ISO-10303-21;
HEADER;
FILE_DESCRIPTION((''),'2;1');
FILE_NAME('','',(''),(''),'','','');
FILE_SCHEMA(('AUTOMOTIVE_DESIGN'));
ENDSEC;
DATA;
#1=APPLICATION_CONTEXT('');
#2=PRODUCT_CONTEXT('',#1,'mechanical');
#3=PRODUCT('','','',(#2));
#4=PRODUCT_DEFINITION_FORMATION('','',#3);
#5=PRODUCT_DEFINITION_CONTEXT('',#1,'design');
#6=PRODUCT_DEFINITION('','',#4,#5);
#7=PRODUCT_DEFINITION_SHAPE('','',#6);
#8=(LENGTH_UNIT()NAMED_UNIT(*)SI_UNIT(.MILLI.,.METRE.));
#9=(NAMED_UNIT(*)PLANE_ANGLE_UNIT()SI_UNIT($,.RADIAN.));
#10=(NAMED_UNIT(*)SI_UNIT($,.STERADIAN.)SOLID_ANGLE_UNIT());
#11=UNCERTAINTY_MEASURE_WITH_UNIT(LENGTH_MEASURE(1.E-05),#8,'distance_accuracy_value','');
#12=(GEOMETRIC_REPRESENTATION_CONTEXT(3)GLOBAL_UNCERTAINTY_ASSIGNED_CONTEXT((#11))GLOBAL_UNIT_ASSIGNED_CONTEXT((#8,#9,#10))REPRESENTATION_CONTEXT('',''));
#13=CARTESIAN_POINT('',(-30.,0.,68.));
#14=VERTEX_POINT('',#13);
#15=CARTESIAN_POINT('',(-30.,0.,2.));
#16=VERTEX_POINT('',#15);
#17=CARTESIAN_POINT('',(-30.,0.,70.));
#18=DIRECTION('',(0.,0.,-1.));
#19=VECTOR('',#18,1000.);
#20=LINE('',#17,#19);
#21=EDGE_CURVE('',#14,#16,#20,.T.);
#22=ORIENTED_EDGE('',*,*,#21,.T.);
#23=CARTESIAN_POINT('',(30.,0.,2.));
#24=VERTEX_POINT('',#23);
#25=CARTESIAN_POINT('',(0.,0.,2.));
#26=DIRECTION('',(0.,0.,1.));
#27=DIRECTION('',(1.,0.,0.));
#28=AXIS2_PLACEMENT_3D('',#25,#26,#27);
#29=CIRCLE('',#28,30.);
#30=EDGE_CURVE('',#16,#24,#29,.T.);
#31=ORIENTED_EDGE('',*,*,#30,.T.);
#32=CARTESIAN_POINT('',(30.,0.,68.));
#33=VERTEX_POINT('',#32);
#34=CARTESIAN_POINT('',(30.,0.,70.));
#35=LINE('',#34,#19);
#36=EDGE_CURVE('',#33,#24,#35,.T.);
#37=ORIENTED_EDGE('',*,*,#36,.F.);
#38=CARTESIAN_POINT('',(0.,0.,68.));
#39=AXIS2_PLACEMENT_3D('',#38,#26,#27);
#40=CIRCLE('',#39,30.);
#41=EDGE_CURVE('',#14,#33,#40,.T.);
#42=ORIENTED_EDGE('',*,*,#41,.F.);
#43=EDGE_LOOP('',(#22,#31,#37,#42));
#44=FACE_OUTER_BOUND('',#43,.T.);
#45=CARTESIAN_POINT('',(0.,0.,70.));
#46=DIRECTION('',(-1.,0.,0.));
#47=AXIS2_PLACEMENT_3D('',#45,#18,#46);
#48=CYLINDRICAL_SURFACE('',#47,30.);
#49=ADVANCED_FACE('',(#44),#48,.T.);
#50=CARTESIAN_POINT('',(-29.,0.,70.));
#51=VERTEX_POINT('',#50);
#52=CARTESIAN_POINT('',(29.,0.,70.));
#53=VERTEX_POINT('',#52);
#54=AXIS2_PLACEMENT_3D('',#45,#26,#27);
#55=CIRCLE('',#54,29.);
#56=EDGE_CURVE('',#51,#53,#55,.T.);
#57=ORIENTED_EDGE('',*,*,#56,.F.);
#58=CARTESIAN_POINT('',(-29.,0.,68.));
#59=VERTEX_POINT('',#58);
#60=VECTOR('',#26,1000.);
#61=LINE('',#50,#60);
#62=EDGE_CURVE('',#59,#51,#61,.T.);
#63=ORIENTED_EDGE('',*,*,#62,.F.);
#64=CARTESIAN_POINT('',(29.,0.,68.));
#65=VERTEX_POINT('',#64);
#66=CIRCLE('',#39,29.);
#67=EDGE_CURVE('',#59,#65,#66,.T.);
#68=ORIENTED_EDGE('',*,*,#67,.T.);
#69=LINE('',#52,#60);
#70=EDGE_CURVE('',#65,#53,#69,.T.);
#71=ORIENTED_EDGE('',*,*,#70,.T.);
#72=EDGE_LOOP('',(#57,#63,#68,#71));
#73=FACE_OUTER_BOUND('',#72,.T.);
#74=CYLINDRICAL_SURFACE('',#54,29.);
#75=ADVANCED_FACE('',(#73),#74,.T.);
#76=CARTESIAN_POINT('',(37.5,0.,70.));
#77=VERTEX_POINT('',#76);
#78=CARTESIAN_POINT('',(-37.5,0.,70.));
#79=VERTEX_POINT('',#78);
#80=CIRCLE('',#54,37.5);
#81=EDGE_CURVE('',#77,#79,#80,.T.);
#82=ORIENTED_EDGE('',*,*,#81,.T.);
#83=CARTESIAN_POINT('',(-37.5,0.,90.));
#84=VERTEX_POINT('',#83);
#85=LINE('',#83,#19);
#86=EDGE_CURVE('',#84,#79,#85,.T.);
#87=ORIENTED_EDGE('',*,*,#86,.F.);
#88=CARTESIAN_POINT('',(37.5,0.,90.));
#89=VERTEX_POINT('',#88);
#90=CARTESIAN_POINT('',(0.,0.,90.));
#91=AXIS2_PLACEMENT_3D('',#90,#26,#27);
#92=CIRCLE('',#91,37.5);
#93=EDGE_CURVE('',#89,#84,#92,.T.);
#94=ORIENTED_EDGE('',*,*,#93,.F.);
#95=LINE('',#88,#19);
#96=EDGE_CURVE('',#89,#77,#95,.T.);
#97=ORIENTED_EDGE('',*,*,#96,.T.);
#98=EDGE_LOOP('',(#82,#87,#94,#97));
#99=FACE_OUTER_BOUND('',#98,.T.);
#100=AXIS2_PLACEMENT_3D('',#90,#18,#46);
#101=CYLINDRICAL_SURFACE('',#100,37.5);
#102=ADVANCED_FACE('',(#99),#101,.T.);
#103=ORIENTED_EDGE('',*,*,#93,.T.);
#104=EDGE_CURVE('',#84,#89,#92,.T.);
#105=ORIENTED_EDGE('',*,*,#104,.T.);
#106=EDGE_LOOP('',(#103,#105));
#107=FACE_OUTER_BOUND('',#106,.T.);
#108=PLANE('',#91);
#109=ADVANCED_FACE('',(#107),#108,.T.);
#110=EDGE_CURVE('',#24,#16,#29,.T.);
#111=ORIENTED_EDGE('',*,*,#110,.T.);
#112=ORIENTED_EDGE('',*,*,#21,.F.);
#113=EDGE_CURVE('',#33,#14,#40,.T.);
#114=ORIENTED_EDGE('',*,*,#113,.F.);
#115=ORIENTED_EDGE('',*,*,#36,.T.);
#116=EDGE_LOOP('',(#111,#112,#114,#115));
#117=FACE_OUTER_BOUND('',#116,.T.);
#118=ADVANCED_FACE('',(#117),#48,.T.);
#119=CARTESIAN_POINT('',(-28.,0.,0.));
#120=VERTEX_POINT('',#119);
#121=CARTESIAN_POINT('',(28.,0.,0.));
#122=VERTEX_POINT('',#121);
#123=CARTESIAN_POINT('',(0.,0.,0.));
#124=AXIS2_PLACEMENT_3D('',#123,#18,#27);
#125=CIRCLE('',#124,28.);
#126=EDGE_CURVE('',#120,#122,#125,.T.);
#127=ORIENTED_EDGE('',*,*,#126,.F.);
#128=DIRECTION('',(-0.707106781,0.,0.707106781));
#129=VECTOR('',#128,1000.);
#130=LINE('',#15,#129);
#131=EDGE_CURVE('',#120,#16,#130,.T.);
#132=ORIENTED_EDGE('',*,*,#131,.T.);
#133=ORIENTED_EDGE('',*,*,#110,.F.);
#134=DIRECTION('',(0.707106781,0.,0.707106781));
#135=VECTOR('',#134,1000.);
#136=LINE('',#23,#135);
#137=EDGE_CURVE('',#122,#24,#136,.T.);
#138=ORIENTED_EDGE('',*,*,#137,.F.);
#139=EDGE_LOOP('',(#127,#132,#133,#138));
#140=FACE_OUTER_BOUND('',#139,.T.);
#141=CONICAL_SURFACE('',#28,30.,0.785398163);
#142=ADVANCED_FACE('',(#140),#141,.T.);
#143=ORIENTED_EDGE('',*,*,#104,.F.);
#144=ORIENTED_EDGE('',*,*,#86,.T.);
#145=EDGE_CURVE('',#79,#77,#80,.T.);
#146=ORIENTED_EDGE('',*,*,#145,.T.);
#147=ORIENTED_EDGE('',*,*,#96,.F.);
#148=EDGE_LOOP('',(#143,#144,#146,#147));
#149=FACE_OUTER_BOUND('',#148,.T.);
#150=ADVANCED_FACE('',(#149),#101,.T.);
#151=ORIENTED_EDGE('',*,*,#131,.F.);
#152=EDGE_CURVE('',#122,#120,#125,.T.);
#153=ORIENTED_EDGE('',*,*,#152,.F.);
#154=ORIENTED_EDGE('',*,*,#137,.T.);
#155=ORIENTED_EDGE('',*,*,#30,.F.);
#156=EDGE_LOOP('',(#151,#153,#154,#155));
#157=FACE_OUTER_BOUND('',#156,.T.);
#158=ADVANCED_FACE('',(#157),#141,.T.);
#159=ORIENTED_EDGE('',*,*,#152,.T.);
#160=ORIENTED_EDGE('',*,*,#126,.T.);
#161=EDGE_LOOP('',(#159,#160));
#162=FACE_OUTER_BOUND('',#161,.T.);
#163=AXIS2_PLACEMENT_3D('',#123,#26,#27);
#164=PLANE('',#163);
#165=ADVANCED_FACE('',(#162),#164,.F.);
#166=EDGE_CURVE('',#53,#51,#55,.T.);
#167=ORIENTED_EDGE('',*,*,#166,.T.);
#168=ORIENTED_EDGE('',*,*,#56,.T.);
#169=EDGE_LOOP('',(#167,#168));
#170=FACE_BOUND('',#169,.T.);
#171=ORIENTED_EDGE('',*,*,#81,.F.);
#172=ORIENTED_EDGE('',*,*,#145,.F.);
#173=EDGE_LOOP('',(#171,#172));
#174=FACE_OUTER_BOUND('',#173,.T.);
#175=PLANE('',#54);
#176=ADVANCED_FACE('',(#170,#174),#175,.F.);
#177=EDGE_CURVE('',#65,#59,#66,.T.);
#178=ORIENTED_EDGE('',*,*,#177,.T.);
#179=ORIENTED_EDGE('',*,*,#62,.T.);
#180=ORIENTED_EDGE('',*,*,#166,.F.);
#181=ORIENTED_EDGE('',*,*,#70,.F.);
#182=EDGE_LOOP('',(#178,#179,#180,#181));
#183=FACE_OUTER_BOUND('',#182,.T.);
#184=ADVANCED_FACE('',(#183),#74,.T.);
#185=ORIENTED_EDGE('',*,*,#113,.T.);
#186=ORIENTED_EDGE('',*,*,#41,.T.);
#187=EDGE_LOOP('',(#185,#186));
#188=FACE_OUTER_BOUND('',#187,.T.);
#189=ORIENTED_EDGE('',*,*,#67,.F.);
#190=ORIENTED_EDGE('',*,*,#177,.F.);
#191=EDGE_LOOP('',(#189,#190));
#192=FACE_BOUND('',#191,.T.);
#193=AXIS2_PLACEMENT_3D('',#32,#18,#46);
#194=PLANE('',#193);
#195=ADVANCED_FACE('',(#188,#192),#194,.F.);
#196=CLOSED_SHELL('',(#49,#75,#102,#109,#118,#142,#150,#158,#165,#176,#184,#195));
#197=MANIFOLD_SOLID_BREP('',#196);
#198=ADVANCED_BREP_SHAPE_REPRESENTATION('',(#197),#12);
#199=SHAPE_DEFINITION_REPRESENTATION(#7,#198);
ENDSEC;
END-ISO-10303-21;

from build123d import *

# Parameters (mm, degrees)
SKETCH_1_R      = 30
EXTRUDE_1_DEPTH = 70
SKETCH_2_R      = 37.5
EXTRUDE_2_DEPTH = 20
CHAMFER_2_SIZE  = 2
SKETCH_3_W      = 1
SKETCH_3_H      = 2


with BuildPart() as part:
    # 草图1 → 凸台-拉伸1 (new body)
    with BuildSketch(Plane.XY):
        Circle(SKETCH_1_R)
    extrude(amount=EXTRUDE_1_DEPTH)

    # 草图2 → 凸台-拉伸2 (add)
    with BuildSketch(Plane.XY.offset(70)):
        Circle(SKETCH_2_R)
    extrude(amount=EXTRUDE_2_DEPTH)

    # 倒角2
    chamfer_2_edges = [part.edges().sort_by_distance(p)[0] for p in [
        (-30, 0, 0),
    ]]
    chamfer(chamfer_2_edges, length=CHAMFER_2_SIZE)

    # 草图3 → 切除-旋转1 (revolve, cut)
    with BuildSketch(Plane(origin=(0, 0, 0), x_dir=(1, 0, 0), z_dir=(0, 1, 0))):
        with Locations((29.5, -69)):
            Rectangle(SKETCH_3_W, SKETCH_3_H)
    revolve(axis=Axis((0, 0, 70), (0, 0, -1)), mode=Mode.SUBTRACT)


solid = part.part
